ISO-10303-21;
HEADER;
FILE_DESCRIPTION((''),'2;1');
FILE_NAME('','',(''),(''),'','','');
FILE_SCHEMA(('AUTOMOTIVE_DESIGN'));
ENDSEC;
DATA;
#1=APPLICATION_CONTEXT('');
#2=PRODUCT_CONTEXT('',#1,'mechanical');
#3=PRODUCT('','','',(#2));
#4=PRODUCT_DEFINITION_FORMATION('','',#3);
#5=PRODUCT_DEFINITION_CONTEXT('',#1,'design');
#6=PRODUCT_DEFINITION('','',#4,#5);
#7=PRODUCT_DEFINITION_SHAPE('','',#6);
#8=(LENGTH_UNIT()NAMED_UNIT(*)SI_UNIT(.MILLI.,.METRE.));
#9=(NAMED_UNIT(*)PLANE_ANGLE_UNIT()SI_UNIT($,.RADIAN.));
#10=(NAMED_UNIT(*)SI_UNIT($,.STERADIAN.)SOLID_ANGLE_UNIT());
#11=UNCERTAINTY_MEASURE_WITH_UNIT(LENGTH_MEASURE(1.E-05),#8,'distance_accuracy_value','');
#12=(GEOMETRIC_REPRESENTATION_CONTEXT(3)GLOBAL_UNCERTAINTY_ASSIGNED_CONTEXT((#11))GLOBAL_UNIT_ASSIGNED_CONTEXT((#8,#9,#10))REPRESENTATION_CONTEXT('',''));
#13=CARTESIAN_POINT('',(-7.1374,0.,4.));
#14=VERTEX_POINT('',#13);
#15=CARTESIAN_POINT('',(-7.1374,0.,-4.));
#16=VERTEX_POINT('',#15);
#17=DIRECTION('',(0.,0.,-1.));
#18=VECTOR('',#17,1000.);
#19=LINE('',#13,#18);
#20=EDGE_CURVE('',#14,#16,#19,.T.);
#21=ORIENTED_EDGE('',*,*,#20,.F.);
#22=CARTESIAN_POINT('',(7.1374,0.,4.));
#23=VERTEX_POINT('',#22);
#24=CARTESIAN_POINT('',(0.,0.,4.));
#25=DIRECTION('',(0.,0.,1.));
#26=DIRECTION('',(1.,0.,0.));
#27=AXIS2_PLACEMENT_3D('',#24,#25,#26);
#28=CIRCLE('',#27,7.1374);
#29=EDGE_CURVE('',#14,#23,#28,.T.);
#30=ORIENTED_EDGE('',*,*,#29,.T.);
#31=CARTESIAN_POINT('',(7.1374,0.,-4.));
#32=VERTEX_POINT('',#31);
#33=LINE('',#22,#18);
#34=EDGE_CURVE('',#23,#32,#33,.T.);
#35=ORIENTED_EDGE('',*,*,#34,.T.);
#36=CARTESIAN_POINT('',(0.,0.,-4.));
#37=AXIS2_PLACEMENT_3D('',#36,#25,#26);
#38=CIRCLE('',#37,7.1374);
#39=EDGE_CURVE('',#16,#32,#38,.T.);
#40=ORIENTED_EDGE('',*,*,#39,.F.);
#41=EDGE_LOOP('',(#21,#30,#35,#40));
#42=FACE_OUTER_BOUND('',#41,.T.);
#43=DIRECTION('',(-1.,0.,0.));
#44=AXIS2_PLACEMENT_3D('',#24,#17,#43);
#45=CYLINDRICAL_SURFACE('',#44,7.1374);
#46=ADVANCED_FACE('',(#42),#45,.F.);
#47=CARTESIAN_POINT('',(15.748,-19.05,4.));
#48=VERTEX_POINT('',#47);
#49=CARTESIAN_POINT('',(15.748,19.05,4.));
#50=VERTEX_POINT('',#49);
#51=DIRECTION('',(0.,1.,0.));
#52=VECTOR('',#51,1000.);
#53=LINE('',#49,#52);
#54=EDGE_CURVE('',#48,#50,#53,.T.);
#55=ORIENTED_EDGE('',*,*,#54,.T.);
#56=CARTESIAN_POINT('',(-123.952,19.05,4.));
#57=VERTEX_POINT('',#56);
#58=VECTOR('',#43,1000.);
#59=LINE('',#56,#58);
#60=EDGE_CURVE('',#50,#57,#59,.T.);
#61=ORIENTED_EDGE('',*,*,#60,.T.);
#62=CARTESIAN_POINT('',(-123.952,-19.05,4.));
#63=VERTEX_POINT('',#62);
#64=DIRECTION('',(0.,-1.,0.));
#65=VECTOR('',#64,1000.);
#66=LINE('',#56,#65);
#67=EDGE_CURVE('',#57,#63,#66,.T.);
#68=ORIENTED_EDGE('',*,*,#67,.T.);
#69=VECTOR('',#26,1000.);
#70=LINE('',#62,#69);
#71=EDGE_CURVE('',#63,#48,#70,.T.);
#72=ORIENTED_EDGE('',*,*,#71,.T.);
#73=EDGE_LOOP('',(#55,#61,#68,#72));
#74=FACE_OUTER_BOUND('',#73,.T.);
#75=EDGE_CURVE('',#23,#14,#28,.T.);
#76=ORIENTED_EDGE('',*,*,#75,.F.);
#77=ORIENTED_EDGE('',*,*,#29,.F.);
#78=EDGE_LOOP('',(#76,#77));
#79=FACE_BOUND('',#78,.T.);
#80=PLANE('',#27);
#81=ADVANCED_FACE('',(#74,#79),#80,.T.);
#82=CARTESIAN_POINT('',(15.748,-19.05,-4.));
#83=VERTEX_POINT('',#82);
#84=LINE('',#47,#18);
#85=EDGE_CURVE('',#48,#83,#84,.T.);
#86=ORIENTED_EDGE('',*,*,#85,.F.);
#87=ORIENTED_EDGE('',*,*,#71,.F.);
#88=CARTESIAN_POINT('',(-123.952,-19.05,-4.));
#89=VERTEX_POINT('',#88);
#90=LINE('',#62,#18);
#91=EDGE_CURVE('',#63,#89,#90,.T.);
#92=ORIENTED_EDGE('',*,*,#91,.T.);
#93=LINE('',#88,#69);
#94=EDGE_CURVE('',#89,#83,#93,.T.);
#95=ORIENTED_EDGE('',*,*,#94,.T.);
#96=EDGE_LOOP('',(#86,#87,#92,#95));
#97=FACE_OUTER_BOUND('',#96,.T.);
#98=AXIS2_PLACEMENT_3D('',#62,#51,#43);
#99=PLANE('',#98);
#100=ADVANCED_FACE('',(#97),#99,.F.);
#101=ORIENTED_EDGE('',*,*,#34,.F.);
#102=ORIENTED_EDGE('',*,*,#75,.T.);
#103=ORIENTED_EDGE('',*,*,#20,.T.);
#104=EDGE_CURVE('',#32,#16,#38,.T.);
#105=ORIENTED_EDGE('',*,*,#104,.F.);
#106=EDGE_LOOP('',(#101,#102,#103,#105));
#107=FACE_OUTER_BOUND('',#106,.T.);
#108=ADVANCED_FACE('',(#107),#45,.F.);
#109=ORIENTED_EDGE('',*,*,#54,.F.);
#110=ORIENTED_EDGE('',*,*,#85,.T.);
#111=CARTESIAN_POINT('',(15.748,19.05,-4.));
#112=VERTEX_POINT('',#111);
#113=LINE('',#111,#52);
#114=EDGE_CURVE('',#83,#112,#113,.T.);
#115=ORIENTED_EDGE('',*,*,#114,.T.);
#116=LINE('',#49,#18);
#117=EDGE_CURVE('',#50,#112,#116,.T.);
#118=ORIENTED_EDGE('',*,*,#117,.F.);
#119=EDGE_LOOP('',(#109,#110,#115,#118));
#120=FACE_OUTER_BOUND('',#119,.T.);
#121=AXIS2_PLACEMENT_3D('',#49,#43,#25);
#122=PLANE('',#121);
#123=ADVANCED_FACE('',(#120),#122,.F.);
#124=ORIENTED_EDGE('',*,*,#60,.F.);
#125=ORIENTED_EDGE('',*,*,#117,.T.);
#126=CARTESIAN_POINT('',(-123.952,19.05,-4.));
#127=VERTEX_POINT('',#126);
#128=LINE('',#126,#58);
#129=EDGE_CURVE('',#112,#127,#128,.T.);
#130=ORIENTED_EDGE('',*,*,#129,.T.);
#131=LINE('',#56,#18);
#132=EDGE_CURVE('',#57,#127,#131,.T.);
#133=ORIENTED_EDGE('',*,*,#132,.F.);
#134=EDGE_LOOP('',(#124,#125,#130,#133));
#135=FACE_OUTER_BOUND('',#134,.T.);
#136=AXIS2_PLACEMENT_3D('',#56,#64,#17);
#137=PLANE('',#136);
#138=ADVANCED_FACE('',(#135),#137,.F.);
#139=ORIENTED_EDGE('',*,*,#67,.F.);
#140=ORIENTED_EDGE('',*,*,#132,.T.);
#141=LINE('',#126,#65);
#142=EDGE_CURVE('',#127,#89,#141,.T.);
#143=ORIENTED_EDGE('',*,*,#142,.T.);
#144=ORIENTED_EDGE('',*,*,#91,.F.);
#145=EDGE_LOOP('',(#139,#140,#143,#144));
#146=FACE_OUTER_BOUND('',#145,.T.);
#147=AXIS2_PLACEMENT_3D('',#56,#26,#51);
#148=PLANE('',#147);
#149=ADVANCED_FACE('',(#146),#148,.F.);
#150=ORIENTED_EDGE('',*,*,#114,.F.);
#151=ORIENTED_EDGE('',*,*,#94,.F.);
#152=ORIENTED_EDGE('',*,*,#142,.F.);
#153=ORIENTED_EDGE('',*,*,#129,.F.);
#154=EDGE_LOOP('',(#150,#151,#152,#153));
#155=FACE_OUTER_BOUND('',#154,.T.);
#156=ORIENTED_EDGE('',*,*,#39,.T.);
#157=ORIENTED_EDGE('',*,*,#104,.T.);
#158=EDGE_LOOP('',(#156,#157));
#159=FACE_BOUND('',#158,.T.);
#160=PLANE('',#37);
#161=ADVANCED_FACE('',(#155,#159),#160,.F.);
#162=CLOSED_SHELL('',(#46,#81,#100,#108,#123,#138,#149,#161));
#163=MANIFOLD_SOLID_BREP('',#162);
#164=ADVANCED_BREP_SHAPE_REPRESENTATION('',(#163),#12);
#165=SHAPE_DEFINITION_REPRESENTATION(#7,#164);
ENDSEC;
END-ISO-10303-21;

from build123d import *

# Parameters (mm, degrees)
SKETCH1_W           = 139.7
SKETCH1_H           = 38.1
SKETCH1_R           = 7.1374
BOSS_EXTRUDE1_DEPTH = 4


with BuildPart() as part:
    # Sketch1 → Boss-Extrude1 (new, symmetric)
    with BuildSketch(Plane.XY):
        with Locations((-54.102, 0)):
            Rectangle(SKETCH1_W, SKETCH1_H)
        Circle(SKETCH1_R, mode=Mode.SUBTRACT)
    extrude(amount=BOSS_EXTRUDE1_DEPTH, both=True)


solid = part.part
